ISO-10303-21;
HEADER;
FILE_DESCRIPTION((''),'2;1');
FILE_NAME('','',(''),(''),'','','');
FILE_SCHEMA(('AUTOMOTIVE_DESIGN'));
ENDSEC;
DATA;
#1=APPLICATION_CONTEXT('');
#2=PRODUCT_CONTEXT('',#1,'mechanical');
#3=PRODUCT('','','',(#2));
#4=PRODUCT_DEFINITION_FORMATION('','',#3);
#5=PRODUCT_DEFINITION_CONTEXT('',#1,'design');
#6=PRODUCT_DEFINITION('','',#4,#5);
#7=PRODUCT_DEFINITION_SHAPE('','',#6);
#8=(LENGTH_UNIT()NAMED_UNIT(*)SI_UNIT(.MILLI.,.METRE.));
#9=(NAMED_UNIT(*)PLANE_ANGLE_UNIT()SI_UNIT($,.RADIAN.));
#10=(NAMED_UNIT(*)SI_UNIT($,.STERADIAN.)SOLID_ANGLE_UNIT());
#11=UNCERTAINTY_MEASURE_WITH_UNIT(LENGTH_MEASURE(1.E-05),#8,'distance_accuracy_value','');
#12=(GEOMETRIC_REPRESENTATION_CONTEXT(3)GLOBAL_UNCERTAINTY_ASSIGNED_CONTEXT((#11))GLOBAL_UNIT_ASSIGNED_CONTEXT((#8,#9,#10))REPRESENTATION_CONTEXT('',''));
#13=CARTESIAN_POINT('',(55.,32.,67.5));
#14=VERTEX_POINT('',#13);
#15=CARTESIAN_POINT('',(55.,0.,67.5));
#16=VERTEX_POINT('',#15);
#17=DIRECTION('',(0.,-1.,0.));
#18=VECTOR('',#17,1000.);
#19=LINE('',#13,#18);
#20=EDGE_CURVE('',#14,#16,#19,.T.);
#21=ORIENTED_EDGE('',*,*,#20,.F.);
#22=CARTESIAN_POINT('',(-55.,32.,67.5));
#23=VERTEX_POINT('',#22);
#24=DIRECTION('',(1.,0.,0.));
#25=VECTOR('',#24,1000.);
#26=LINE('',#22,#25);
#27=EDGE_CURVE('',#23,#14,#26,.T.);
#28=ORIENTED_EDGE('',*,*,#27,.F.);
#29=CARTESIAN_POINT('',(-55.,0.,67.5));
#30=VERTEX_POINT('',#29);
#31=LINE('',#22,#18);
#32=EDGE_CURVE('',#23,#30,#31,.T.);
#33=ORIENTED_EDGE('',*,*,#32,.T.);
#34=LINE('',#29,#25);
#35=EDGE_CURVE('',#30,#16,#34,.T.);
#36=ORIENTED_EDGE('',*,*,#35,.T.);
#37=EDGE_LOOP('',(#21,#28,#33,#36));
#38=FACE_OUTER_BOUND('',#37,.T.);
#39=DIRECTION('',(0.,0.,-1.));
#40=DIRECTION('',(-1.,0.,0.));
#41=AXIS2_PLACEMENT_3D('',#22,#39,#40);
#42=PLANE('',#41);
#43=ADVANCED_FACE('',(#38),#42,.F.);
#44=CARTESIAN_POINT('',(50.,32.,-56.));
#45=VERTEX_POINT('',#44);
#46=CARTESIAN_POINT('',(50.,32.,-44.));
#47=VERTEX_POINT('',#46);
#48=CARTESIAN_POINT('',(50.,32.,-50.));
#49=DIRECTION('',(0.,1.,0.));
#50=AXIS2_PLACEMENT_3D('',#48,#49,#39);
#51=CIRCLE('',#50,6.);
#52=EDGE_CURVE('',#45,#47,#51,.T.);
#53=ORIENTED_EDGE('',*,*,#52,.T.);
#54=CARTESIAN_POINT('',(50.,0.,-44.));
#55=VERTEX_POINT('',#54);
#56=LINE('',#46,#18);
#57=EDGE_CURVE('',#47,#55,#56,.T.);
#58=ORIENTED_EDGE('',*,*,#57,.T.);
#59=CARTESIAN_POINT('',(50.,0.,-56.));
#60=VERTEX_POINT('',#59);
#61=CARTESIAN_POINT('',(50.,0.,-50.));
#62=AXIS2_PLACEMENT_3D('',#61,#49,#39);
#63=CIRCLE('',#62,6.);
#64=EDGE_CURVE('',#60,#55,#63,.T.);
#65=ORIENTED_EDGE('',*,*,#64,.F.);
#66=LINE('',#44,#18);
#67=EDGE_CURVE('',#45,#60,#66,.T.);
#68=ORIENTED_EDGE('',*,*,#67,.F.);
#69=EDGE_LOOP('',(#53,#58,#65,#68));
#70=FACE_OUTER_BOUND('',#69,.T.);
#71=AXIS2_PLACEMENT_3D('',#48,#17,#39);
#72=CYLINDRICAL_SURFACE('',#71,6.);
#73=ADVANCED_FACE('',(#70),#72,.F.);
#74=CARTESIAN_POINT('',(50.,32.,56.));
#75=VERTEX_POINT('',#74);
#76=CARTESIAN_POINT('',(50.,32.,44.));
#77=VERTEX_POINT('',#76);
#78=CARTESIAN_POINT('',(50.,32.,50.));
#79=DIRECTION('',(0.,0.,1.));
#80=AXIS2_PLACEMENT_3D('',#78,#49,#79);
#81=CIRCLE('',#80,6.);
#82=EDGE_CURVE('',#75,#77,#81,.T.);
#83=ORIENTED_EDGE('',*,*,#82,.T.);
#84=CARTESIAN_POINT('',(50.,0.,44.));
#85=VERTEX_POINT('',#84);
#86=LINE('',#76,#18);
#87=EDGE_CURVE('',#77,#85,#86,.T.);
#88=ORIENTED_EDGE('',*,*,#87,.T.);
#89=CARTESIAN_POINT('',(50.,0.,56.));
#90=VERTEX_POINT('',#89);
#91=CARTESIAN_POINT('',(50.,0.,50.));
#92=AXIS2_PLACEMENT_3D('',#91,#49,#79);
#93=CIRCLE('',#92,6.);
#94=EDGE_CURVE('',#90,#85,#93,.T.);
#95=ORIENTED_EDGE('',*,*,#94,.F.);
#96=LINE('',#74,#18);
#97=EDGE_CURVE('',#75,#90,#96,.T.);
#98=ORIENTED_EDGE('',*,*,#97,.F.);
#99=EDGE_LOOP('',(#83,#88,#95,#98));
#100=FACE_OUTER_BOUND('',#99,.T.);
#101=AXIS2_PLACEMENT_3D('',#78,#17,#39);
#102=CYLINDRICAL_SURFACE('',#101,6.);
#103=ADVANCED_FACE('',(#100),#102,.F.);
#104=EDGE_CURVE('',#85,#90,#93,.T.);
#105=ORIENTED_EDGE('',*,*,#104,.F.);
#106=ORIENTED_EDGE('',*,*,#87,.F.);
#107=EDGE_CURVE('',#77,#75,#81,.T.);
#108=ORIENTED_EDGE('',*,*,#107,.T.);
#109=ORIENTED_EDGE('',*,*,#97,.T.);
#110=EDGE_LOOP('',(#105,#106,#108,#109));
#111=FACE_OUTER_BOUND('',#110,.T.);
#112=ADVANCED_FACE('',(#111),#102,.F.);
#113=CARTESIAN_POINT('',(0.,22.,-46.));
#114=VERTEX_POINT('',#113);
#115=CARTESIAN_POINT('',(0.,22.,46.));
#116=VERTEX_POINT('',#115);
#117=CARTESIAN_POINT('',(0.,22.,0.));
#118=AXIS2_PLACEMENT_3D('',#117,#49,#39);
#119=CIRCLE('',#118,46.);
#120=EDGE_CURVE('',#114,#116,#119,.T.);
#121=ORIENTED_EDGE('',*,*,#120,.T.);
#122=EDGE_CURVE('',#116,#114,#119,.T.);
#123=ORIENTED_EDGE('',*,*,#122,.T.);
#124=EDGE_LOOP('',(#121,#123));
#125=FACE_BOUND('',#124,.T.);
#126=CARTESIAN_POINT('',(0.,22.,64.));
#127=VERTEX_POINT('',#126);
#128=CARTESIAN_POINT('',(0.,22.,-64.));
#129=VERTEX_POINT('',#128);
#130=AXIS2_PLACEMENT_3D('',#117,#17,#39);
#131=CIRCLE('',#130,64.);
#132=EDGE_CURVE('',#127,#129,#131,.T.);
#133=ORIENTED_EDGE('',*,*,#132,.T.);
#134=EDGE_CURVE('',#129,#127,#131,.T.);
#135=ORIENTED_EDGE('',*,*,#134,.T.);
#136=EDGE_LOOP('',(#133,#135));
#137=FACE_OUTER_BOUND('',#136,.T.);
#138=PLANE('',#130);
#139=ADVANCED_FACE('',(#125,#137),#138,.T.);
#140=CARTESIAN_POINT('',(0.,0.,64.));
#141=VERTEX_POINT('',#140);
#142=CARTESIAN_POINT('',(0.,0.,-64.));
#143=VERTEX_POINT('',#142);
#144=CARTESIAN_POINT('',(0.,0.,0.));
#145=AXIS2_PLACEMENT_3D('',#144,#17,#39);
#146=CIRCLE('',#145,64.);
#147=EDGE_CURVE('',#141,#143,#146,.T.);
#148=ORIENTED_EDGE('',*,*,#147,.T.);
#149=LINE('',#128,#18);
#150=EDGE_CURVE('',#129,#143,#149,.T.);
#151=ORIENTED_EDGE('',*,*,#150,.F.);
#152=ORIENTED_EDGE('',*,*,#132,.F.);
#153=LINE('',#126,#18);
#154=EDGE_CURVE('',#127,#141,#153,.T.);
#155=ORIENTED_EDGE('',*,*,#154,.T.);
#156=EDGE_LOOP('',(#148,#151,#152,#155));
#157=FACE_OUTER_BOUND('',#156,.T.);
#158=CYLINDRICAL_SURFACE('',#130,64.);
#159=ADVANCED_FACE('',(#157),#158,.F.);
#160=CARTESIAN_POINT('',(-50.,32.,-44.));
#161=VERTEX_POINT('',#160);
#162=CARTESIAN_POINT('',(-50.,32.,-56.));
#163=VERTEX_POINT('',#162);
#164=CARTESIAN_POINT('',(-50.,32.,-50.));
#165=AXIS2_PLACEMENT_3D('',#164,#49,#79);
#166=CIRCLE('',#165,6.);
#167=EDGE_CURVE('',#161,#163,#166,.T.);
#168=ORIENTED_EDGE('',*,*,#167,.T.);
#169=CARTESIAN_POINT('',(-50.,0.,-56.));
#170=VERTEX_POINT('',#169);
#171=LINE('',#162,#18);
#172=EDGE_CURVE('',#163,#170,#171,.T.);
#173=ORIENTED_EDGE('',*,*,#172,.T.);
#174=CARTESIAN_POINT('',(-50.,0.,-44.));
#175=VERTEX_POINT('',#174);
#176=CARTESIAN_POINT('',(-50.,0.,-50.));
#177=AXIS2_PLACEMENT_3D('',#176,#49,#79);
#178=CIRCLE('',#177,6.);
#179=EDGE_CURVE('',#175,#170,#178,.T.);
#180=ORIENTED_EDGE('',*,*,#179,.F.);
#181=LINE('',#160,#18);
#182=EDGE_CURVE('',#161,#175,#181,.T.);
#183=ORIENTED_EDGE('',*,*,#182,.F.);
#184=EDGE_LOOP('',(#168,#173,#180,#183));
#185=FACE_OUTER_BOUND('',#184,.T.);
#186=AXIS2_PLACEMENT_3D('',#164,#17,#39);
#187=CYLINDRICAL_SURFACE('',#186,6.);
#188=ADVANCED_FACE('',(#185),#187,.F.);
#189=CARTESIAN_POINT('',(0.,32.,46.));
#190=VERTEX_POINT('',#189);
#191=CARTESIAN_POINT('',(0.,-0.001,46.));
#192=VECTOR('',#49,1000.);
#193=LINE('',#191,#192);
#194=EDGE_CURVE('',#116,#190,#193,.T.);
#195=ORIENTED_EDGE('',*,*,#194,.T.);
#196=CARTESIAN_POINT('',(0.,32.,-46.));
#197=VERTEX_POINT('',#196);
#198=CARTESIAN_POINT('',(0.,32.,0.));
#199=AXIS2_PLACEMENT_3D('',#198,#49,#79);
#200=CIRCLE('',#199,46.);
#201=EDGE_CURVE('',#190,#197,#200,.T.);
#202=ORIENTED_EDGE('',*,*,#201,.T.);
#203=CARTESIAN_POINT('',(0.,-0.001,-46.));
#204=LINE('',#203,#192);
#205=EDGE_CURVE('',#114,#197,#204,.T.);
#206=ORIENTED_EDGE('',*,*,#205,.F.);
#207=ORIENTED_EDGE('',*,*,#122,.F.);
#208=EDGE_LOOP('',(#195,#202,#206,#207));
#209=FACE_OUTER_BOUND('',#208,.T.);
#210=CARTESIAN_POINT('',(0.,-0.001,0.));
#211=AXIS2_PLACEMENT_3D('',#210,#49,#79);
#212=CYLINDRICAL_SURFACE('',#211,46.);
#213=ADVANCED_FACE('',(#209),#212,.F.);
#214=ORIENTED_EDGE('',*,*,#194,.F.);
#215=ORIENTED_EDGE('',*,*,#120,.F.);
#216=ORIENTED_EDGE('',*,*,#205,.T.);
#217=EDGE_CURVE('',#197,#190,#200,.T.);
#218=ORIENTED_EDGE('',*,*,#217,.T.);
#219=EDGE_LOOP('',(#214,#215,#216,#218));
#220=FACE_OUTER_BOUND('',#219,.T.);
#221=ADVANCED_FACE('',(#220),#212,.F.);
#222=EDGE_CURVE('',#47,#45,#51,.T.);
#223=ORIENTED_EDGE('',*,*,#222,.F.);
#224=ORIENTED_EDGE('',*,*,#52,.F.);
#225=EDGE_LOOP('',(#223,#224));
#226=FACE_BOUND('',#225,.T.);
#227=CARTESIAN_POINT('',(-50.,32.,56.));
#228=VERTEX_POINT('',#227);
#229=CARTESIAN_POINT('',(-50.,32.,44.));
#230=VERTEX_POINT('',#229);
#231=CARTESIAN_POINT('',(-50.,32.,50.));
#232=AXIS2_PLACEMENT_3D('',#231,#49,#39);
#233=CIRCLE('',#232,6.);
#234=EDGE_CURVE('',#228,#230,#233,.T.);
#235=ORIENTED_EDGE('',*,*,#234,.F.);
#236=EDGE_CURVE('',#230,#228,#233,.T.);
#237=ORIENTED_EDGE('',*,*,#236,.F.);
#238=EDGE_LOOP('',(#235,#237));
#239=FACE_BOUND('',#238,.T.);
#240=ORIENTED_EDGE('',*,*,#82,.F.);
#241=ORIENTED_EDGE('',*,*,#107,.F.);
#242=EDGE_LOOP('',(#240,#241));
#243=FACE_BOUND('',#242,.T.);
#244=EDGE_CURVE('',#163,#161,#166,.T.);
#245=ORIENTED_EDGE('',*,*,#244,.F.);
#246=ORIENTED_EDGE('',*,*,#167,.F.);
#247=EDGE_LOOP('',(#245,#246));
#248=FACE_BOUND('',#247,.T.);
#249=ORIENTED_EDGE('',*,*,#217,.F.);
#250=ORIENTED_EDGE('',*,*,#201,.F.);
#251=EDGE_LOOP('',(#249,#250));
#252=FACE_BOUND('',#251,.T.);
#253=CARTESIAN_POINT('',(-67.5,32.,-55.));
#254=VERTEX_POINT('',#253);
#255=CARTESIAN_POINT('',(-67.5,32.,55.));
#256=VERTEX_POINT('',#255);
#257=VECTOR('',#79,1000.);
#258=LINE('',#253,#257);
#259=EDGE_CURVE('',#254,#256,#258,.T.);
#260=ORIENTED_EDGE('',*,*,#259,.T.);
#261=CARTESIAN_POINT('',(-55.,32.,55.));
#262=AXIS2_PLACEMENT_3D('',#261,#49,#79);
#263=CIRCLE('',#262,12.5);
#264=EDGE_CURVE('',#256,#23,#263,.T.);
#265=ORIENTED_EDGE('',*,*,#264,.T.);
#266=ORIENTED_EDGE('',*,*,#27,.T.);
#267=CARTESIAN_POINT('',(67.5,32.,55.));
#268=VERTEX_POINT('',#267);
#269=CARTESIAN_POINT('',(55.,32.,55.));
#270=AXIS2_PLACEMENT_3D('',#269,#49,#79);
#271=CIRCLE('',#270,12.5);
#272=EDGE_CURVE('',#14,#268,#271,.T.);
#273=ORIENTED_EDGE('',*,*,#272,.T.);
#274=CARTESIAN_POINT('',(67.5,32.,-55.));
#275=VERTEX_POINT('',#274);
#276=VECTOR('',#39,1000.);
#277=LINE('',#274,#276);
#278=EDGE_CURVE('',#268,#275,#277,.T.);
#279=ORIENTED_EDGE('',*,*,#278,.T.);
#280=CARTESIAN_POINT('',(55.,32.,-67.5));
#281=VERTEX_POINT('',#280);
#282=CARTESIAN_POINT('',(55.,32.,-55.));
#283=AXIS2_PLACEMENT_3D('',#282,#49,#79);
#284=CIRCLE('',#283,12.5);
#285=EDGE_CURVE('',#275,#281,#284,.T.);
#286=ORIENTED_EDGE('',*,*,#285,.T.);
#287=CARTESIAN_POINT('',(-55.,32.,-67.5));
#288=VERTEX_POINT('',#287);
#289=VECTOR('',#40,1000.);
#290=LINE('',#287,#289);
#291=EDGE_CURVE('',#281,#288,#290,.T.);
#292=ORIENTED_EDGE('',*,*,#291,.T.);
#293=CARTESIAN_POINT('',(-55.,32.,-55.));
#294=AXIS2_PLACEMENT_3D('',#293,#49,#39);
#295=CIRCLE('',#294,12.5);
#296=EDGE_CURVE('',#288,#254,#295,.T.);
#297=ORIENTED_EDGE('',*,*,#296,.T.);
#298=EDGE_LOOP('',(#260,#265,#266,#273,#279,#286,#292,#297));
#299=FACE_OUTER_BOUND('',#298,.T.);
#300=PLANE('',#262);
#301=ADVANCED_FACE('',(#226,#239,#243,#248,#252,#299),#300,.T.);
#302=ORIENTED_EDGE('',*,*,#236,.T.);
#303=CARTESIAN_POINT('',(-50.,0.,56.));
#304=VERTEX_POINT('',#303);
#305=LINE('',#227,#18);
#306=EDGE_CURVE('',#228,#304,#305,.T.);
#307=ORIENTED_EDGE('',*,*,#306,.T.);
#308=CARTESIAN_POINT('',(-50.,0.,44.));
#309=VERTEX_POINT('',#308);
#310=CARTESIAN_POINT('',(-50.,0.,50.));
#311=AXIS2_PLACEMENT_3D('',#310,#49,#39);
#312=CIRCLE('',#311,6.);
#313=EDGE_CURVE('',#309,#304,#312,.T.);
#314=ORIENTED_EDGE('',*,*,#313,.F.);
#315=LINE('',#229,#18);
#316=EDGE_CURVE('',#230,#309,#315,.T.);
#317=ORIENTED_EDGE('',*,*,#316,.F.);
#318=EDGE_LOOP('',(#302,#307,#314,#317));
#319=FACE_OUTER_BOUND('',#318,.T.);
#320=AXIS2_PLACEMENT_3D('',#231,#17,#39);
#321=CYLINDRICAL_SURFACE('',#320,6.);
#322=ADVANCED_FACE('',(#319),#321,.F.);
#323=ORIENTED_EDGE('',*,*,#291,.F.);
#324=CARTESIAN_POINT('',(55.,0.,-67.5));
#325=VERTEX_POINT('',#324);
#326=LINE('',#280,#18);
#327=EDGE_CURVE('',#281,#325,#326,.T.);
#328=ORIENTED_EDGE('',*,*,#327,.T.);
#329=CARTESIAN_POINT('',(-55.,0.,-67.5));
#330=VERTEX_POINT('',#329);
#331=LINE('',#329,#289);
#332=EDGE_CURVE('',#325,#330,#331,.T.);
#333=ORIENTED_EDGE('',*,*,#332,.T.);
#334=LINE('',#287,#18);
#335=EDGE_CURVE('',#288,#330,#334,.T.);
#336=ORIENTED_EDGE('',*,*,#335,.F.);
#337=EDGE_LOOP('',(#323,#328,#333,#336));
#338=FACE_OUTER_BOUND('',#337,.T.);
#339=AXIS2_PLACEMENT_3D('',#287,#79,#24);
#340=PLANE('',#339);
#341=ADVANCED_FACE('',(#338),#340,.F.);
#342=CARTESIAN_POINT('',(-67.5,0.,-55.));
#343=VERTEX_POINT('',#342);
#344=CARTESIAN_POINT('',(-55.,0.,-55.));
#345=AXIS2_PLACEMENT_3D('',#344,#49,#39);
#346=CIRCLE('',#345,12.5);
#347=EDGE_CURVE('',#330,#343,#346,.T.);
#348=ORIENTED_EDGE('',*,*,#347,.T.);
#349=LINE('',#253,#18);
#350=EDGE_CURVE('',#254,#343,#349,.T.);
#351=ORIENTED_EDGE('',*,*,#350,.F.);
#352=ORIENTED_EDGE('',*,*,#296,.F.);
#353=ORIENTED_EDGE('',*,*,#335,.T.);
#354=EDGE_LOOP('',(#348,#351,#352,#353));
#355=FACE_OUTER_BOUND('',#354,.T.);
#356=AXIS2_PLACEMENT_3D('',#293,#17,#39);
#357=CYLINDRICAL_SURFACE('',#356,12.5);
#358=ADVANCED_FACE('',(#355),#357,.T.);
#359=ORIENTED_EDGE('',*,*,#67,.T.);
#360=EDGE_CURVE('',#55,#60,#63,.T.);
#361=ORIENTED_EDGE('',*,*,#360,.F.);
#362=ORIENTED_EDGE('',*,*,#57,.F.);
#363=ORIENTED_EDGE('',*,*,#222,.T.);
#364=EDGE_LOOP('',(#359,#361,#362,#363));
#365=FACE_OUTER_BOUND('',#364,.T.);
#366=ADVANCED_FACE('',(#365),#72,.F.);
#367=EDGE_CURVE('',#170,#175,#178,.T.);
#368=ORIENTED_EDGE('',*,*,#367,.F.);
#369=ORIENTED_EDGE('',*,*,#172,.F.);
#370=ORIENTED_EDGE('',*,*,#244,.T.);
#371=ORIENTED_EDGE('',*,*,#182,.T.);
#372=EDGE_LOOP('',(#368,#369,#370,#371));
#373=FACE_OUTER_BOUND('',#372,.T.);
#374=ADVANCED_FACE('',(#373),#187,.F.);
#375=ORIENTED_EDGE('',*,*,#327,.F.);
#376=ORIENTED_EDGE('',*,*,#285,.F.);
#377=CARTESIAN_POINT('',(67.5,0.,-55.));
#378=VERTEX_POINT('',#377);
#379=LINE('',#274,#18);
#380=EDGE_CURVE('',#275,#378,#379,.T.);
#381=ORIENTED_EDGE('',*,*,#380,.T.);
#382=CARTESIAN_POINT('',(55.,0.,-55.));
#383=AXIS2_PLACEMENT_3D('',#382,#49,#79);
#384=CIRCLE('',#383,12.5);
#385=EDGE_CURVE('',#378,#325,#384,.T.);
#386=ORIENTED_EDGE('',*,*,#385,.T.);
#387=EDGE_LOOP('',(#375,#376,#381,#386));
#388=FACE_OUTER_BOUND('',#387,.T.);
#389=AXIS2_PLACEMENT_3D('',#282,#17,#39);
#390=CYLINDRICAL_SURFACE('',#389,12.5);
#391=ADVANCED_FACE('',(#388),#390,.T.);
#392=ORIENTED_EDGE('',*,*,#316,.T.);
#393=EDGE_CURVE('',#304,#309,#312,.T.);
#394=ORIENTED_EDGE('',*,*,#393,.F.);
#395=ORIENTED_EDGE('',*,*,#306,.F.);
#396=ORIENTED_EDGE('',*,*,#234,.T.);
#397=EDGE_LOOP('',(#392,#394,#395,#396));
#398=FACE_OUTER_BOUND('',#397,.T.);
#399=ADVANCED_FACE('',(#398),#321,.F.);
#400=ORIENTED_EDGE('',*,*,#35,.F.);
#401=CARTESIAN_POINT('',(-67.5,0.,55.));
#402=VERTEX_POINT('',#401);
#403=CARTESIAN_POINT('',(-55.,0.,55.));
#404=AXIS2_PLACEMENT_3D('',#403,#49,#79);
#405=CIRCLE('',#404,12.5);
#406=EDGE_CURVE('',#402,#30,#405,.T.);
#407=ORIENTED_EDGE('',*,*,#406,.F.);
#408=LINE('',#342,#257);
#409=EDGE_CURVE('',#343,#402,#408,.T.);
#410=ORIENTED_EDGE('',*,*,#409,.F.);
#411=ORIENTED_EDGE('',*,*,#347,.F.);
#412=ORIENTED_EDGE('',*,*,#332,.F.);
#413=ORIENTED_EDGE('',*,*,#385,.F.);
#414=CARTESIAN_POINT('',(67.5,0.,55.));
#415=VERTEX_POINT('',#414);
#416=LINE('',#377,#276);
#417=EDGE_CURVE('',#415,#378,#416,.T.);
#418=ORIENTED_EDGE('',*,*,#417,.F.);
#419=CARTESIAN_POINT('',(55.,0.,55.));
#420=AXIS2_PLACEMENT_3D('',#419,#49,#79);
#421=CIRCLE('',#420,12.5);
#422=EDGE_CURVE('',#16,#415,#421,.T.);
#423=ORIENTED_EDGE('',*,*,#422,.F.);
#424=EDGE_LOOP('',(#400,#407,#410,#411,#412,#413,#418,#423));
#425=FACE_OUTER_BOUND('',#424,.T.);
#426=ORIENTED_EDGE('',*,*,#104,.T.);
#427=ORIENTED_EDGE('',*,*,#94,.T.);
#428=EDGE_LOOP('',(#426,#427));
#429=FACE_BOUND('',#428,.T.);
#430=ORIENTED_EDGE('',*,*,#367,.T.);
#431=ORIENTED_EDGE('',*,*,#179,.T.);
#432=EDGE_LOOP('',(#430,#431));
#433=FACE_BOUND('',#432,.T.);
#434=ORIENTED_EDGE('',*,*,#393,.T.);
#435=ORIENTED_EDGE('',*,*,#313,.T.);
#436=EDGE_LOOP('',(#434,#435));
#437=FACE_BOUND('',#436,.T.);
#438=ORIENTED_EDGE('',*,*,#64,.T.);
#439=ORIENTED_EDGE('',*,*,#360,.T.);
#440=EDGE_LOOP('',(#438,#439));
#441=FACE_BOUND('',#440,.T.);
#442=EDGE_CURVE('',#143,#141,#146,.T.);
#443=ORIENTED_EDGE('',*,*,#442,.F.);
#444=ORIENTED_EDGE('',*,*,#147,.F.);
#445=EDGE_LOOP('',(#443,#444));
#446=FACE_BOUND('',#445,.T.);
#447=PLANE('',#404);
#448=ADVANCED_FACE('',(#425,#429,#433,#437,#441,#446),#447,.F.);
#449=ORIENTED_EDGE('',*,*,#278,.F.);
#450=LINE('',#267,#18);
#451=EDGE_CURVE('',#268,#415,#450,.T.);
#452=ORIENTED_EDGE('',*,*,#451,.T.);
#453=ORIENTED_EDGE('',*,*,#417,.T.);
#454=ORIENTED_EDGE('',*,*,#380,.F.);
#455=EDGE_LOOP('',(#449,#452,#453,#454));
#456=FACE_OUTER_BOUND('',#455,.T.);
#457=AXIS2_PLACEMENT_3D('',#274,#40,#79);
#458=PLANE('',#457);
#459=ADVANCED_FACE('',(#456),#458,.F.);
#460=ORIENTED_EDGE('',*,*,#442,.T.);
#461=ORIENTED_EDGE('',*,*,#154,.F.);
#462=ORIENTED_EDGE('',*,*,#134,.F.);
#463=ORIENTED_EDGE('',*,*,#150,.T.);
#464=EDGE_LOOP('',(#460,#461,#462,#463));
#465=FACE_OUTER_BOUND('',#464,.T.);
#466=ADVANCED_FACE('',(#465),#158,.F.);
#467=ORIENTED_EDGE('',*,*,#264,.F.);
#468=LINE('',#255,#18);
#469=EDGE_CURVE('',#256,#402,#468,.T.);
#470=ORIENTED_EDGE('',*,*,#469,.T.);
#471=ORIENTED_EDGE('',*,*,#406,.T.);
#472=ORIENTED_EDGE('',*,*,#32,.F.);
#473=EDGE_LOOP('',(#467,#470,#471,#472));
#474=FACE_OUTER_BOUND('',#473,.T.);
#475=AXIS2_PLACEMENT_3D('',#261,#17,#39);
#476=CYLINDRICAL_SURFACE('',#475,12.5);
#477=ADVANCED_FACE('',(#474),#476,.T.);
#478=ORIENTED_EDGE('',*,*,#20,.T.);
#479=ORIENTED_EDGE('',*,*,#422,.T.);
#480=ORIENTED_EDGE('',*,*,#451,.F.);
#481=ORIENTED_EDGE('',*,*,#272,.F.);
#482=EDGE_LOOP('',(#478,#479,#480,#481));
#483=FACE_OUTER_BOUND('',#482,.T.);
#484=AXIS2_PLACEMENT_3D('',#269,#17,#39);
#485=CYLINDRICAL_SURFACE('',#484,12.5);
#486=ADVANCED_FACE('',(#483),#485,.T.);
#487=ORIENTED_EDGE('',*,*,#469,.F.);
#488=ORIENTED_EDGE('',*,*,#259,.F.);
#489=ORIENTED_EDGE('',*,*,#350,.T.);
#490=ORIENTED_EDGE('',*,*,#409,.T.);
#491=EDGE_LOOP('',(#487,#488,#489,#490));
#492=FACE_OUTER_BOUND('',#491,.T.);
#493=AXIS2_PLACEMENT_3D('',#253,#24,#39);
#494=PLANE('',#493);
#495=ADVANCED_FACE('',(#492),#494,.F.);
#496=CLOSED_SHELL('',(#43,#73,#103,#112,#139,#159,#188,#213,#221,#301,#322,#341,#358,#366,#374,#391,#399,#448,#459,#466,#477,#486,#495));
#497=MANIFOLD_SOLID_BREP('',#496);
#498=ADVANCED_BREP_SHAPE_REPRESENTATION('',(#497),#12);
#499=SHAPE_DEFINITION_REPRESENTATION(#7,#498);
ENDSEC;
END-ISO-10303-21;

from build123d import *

# Parameters (mm, degrees)
BASE_PLATE_PROFILE_R        = 6
BASE_PLATE_135X135X32_DEPTH = 32
THROUGH_BORE_92_REACH       = 102.68
THROUGH_BORE_PROFILE_R      = 46
COUNTERBORE_PROFILE_R       = 64
COUNTERBORE_128X22_DEPTH    = 22


with BuildPart() as part:
    # Base Plate Profile → Base Plate 135x135x32 (new body)
    with BuildSketch(Plane(origin=(0, 0, 0), x_dir=(1, 0, 0), z_dir=(0, 1, 0))):
        with BuildLine():
            Line((-55, 67.5), (55, 67.5))
            ThreePointArc((55, 67.5), (63.838834765, 63.838834765), (67.5, 55))
            Line((67.5, 55), (67.5, -55))
            ThreePointArc((67.5, -55), (63.838834765, -63.838834765), (55, -67.5))
            Line((55, -67.5), (-55, -67.5))
            ThreePointArc((-55, -67.5), (-63.838834765, -63.838834765), (-67.5, -55))
            Line((-67.5, -55), (-67.5, 55))
            ThreePointArc((-67.5, 55), (-63.838834765, 63.838834765), (-55, 67.5))
        make_face()
        with Locations(Location((-50, 50, 0), (0, 0, 270))):
            Circle(BASE_PLATE_PROFILE_R, mode=Mode.SUBTRACT)
        with Locations(Location((50, 50, 0), (0, 0, 90))):
            Circle(BASE_PLATE_PROFILE_R, mode=Mode.SUBTRACT)
        with Locations(Location((50, -50, 0), (0, 0, 270))):
            Circle(BASE_PLATE_PROFILE_R, mode=Mode.SUBTRACT)
        with Locations(Location((-50, -50, 0), (0, 0, 90))):
            Circle(BASE_PLATE_PROFILE_R, mode=Mode.SUBTRACT)
    extrude(amount=BASE_PLATE_135X135X32_DEPTH)

    # Through Bore Profile → Through Bore Ø92 (cut, up to next)
    with BuildSketch(Plane(origin=(0, 32, 0), x_dir=(1, 0, 0), z_dir=(0, 1, 0)), mode=Mode.PRIVATE) as through_bore_92_sk1:
        with Locations(Location((0, 0, 0), (0, 0, 270))):
            Circle(THROUGH_BORE_PROFILE_R)
    through_bore_92_tool1 = extrude(through_bore_92_sk1.sketch, amount=-THROUGH_BORE_92_REACH, mode=Mode.PRIVATE) & part.part
    add(through_bore_92_tool1.solids().sort_by_distance((0, 32, 0))[0], mode=Mode.SUBTRACT)

    # Counterbore Profile → Counterbore Ø128x22 (cut)
    with BuildSketch(Plane(origin=(0, 0, 0), x_dir=(-1, 0, 0), z_dir=(0, -1, 0))):
        with Locations(Location((0, 0, 0), (0, 0, 90))):
            Circle(COUNTERBORE_PROFILE_R)
    extrude(amount=-COUNTERBORE_128X22_DEPTH, mode=Mode.SUBTRACT)


solid = part.part
